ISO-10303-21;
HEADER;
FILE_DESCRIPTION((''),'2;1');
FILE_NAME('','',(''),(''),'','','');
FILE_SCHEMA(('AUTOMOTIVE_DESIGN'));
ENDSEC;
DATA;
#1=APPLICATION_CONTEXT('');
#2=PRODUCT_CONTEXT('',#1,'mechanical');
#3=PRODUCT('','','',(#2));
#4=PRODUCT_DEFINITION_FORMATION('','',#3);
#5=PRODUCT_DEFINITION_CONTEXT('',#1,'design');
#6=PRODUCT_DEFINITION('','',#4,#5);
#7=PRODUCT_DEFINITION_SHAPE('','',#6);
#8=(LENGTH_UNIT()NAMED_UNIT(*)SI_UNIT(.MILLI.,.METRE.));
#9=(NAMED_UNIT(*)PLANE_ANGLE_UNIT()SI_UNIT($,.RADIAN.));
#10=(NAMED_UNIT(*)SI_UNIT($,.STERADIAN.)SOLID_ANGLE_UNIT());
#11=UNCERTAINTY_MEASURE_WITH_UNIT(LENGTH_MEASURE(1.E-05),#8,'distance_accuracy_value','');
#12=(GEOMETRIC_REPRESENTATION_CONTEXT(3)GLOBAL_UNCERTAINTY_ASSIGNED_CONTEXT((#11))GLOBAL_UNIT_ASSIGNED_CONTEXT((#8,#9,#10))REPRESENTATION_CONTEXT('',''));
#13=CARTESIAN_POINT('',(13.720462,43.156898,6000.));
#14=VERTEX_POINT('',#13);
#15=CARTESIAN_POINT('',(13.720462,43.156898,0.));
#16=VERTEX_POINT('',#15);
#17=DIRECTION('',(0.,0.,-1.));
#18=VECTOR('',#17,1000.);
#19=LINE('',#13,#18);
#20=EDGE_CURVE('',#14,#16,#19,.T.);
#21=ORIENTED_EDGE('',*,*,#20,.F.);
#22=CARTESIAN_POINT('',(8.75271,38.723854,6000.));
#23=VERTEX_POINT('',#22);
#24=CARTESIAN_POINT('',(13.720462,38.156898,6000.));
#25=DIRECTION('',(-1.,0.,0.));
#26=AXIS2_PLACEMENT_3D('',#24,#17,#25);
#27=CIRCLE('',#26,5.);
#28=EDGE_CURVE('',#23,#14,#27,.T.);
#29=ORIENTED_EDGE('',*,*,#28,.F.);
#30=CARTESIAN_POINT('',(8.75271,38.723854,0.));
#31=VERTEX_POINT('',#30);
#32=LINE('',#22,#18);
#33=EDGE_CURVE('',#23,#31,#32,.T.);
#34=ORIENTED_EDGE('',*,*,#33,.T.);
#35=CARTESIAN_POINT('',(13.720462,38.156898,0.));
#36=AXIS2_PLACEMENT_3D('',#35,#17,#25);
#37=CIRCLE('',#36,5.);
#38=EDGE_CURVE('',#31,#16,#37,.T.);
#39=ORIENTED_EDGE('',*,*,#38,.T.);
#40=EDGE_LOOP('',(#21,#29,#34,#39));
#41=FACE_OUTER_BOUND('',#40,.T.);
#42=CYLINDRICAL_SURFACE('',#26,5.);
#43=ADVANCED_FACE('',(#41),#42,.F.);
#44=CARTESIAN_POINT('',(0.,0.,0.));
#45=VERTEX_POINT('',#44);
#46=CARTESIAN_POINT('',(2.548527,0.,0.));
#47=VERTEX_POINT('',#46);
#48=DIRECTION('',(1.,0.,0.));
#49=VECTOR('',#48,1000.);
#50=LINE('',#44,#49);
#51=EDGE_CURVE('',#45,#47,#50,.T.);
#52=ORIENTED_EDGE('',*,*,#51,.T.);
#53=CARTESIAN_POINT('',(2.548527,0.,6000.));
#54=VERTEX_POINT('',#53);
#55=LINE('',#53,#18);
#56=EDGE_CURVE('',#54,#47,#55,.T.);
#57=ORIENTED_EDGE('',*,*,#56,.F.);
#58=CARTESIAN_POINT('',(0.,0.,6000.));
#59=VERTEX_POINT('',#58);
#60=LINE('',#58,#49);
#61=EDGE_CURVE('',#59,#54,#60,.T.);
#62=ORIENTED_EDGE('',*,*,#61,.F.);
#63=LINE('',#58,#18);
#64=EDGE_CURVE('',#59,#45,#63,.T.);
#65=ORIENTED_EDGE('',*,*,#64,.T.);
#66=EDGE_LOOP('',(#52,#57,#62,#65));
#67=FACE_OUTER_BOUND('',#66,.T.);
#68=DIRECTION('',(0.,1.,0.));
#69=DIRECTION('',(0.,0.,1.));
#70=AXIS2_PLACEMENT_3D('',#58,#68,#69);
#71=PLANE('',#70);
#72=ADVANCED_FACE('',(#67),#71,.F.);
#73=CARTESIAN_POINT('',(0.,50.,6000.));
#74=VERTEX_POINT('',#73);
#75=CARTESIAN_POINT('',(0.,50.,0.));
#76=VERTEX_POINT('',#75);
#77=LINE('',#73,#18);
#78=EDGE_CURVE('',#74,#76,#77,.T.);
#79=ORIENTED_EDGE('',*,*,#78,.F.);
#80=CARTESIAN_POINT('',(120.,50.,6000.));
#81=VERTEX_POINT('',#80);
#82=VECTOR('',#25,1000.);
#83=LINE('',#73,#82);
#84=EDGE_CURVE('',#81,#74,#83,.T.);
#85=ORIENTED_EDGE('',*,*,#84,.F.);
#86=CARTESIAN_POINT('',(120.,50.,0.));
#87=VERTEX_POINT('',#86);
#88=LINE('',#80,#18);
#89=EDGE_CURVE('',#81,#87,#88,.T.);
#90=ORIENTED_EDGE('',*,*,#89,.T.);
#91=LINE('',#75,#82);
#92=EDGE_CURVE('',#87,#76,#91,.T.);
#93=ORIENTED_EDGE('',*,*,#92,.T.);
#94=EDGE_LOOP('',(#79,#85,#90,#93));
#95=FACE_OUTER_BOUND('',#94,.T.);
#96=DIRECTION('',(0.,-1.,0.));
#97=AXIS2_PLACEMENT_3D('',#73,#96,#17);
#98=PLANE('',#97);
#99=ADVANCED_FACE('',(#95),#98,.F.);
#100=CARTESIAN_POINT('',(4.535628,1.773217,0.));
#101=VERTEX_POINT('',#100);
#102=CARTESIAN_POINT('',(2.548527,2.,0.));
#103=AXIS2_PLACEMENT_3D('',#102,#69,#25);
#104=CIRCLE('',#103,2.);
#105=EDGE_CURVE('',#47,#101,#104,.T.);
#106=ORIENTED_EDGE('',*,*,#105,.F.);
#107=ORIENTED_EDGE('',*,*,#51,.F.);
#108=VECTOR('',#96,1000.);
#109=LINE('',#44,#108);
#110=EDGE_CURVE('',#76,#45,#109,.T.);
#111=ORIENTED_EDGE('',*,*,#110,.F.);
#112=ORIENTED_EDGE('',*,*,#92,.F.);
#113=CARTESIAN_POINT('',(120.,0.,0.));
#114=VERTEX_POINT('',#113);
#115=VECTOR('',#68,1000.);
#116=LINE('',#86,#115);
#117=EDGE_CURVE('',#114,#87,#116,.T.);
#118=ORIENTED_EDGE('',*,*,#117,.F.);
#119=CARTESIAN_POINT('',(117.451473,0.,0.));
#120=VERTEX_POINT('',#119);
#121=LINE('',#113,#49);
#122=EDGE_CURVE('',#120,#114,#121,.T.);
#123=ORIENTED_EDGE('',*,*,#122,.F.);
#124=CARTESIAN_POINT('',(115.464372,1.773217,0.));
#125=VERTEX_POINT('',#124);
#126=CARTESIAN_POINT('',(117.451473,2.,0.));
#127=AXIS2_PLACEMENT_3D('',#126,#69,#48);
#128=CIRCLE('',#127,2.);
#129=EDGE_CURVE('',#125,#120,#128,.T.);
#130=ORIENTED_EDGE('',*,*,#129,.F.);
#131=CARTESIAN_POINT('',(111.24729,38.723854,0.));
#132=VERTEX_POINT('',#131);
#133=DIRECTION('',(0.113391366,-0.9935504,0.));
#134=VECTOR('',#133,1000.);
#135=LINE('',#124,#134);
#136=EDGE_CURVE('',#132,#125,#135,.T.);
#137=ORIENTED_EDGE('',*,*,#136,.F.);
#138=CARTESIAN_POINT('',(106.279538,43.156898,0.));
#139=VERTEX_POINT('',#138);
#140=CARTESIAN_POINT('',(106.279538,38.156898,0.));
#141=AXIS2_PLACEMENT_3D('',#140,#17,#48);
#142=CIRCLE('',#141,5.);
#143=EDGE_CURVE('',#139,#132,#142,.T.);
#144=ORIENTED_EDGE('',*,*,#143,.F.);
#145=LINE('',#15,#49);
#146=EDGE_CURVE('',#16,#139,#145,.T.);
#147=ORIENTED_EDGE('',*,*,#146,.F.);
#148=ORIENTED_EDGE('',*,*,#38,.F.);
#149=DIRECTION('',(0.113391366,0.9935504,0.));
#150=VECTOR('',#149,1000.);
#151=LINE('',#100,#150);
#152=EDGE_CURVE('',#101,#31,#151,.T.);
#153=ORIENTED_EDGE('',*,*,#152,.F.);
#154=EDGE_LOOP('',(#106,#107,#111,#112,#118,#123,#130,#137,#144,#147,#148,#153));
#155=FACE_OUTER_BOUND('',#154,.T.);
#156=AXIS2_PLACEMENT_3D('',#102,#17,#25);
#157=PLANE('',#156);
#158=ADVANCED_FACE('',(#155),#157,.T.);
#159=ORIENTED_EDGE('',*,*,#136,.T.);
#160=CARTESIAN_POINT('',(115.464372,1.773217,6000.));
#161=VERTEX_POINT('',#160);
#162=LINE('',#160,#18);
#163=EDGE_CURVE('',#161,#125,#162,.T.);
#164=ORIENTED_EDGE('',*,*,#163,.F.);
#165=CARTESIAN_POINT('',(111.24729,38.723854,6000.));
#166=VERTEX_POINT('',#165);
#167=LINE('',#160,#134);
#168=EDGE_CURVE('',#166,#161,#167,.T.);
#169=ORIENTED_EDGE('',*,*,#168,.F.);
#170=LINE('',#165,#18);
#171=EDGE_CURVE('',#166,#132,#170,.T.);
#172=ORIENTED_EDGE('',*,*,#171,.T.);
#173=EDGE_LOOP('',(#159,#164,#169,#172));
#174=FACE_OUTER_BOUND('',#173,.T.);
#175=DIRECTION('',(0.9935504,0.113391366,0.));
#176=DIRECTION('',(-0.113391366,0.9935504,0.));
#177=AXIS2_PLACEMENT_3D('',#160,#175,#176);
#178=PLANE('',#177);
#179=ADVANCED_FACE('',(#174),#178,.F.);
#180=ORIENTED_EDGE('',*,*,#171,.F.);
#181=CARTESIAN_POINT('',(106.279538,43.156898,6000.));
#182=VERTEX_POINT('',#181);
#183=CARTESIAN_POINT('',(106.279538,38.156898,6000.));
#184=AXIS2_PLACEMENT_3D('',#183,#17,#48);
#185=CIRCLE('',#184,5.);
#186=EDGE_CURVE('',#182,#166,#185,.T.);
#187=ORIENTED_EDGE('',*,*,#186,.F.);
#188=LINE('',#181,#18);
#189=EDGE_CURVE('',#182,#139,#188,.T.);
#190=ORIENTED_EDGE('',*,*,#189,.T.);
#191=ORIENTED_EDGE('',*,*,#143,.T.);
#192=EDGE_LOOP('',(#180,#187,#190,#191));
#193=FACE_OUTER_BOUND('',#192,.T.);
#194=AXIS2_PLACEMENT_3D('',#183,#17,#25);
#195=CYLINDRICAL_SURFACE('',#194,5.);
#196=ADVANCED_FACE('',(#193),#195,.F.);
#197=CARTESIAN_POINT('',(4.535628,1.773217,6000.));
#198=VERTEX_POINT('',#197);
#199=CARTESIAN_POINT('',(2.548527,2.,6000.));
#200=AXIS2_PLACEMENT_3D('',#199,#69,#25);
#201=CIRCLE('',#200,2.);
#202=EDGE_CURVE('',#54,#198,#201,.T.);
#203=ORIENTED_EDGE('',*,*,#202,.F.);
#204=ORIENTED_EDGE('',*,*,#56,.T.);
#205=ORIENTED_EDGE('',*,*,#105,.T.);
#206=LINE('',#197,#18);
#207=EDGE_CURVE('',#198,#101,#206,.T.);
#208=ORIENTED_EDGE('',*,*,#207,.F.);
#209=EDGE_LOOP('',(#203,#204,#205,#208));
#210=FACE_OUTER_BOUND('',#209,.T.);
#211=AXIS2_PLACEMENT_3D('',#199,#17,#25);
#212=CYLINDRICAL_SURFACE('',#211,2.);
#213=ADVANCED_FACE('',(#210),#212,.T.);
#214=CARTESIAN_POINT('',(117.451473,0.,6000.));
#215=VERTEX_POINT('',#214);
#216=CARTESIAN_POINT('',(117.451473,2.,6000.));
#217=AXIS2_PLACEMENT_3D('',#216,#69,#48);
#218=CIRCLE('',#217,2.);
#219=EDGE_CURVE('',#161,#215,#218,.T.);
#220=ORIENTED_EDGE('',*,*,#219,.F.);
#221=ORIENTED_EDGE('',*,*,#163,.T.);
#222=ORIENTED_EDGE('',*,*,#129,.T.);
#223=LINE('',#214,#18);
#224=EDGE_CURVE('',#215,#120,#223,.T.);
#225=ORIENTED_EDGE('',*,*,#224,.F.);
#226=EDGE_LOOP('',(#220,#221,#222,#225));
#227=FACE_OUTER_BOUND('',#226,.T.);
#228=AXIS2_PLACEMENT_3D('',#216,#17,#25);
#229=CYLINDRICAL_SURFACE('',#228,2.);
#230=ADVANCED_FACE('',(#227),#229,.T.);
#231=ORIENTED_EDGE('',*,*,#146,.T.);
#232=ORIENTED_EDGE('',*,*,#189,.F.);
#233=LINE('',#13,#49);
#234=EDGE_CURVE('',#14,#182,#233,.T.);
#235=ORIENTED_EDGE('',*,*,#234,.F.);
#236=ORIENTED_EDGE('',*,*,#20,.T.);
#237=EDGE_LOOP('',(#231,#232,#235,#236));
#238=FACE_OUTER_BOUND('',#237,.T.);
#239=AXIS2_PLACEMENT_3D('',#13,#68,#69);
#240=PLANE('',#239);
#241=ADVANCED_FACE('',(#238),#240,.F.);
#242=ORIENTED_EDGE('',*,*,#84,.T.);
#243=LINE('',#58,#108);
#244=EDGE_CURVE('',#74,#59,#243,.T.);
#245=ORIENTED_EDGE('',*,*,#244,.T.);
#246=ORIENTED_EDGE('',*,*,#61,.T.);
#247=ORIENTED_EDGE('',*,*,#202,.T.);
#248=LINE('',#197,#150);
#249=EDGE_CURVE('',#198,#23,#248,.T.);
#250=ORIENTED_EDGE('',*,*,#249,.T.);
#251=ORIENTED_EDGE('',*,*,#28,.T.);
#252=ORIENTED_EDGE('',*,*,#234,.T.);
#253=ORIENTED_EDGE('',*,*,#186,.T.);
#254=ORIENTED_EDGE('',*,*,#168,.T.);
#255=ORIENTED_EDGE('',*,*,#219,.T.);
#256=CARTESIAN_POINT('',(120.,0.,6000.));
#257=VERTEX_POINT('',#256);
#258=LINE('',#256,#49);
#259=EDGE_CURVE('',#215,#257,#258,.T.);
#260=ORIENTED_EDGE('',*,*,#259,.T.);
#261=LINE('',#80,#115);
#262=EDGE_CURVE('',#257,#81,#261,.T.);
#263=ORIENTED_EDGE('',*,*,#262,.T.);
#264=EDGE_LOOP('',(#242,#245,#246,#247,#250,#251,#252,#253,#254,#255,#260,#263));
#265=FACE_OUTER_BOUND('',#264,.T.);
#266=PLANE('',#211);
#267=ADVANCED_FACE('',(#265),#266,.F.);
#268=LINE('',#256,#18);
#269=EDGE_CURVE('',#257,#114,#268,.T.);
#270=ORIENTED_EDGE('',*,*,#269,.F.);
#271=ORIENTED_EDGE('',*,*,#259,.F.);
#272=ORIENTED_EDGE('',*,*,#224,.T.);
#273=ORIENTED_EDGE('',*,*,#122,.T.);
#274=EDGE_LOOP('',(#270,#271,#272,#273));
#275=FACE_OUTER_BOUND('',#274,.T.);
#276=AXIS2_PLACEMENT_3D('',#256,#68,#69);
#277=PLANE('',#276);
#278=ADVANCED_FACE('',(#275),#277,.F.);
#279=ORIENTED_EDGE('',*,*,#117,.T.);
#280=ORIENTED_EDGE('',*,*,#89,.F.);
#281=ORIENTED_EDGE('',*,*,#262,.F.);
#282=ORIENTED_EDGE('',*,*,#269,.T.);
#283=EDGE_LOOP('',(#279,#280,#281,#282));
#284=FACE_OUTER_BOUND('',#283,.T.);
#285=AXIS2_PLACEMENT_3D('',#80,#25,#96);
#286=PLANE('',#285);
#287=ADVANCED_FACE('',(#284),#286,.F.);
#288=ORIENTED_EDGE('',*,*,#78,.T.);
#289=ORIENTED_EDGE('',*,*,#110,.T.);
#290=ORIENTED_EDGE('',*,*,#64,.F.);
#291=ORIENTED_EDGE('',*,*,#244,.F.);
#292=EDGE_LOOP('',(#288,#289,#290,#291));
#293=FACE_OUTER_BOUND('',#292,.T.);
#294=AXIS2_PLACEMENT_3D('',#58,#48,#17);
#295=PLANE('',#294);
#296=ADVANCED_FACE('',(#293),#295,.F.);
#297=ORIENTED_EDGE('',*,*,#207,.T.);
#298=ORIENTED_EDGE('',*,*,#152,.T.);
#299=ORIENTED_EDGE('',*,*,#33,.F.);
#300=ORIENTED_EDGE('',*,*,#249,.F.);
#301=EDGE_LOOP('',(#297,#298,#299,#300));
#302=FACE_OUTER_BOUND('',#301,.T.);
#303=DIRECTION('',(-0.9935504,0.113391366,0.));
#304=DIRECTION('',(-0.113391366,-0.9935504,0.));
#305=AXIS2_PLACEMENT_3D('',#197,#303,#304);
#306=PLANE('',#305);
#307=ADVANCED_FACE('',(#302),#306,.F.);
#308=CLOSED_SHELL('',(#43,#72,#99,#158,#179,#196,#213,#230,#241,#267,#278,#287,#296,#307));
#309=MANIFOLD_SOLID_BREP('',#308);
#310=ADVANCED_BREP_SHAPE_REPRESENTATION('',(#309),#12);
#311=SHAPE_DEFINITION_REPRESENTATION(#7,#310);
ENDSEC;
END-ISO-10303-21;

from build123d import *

# Parameters (mm, degrees)
BOSS_EXTRUDE1_DEPTH = 6000


with BuildPart() as part:
    # Sketch1 → Boss-Extrude1 (new body)
    with BuildSketch(Plane.XY):
        with BuildLine():
            Line((0, 0), (0, 50))
            Line((0, 50), (120, 50))
            Line((120, 50), (120, 0))
            Line((120, 0), (117.451472673, 0))
            ThreePointArc((117.451472673, 0), (116.119850629, 0.507759157), (115.464371872, 1.773217267))
            Line((115.464371872, 1.773217267), (111.247290138, 38.723854473))
            ThreePointArc((111.247290138, 38.723854473), (109.608593246, 41.887499748), (106.279538137, 43.156897641))
            Line((106.279538137, 43.156897641), (13.720461863, 43.156897641))
            ThreePointArc((13.720461863, 43.156897641), (10.391406754, 41.887499748), (8.752709862, 38.723854473))
            Line((8.752709862, 38.723854473), (4.535628128, 1.773217267))
            ThreePointArc((4.535628128, 1.773217267), (3.880149371, 0.507759157), (2.548527327, 0))
            Line((2.548527327, 0), (0, 0))
        make_face()
    extrude(amount=BOSS_EXTRUDE1_DEPTH)


solid = part.part
